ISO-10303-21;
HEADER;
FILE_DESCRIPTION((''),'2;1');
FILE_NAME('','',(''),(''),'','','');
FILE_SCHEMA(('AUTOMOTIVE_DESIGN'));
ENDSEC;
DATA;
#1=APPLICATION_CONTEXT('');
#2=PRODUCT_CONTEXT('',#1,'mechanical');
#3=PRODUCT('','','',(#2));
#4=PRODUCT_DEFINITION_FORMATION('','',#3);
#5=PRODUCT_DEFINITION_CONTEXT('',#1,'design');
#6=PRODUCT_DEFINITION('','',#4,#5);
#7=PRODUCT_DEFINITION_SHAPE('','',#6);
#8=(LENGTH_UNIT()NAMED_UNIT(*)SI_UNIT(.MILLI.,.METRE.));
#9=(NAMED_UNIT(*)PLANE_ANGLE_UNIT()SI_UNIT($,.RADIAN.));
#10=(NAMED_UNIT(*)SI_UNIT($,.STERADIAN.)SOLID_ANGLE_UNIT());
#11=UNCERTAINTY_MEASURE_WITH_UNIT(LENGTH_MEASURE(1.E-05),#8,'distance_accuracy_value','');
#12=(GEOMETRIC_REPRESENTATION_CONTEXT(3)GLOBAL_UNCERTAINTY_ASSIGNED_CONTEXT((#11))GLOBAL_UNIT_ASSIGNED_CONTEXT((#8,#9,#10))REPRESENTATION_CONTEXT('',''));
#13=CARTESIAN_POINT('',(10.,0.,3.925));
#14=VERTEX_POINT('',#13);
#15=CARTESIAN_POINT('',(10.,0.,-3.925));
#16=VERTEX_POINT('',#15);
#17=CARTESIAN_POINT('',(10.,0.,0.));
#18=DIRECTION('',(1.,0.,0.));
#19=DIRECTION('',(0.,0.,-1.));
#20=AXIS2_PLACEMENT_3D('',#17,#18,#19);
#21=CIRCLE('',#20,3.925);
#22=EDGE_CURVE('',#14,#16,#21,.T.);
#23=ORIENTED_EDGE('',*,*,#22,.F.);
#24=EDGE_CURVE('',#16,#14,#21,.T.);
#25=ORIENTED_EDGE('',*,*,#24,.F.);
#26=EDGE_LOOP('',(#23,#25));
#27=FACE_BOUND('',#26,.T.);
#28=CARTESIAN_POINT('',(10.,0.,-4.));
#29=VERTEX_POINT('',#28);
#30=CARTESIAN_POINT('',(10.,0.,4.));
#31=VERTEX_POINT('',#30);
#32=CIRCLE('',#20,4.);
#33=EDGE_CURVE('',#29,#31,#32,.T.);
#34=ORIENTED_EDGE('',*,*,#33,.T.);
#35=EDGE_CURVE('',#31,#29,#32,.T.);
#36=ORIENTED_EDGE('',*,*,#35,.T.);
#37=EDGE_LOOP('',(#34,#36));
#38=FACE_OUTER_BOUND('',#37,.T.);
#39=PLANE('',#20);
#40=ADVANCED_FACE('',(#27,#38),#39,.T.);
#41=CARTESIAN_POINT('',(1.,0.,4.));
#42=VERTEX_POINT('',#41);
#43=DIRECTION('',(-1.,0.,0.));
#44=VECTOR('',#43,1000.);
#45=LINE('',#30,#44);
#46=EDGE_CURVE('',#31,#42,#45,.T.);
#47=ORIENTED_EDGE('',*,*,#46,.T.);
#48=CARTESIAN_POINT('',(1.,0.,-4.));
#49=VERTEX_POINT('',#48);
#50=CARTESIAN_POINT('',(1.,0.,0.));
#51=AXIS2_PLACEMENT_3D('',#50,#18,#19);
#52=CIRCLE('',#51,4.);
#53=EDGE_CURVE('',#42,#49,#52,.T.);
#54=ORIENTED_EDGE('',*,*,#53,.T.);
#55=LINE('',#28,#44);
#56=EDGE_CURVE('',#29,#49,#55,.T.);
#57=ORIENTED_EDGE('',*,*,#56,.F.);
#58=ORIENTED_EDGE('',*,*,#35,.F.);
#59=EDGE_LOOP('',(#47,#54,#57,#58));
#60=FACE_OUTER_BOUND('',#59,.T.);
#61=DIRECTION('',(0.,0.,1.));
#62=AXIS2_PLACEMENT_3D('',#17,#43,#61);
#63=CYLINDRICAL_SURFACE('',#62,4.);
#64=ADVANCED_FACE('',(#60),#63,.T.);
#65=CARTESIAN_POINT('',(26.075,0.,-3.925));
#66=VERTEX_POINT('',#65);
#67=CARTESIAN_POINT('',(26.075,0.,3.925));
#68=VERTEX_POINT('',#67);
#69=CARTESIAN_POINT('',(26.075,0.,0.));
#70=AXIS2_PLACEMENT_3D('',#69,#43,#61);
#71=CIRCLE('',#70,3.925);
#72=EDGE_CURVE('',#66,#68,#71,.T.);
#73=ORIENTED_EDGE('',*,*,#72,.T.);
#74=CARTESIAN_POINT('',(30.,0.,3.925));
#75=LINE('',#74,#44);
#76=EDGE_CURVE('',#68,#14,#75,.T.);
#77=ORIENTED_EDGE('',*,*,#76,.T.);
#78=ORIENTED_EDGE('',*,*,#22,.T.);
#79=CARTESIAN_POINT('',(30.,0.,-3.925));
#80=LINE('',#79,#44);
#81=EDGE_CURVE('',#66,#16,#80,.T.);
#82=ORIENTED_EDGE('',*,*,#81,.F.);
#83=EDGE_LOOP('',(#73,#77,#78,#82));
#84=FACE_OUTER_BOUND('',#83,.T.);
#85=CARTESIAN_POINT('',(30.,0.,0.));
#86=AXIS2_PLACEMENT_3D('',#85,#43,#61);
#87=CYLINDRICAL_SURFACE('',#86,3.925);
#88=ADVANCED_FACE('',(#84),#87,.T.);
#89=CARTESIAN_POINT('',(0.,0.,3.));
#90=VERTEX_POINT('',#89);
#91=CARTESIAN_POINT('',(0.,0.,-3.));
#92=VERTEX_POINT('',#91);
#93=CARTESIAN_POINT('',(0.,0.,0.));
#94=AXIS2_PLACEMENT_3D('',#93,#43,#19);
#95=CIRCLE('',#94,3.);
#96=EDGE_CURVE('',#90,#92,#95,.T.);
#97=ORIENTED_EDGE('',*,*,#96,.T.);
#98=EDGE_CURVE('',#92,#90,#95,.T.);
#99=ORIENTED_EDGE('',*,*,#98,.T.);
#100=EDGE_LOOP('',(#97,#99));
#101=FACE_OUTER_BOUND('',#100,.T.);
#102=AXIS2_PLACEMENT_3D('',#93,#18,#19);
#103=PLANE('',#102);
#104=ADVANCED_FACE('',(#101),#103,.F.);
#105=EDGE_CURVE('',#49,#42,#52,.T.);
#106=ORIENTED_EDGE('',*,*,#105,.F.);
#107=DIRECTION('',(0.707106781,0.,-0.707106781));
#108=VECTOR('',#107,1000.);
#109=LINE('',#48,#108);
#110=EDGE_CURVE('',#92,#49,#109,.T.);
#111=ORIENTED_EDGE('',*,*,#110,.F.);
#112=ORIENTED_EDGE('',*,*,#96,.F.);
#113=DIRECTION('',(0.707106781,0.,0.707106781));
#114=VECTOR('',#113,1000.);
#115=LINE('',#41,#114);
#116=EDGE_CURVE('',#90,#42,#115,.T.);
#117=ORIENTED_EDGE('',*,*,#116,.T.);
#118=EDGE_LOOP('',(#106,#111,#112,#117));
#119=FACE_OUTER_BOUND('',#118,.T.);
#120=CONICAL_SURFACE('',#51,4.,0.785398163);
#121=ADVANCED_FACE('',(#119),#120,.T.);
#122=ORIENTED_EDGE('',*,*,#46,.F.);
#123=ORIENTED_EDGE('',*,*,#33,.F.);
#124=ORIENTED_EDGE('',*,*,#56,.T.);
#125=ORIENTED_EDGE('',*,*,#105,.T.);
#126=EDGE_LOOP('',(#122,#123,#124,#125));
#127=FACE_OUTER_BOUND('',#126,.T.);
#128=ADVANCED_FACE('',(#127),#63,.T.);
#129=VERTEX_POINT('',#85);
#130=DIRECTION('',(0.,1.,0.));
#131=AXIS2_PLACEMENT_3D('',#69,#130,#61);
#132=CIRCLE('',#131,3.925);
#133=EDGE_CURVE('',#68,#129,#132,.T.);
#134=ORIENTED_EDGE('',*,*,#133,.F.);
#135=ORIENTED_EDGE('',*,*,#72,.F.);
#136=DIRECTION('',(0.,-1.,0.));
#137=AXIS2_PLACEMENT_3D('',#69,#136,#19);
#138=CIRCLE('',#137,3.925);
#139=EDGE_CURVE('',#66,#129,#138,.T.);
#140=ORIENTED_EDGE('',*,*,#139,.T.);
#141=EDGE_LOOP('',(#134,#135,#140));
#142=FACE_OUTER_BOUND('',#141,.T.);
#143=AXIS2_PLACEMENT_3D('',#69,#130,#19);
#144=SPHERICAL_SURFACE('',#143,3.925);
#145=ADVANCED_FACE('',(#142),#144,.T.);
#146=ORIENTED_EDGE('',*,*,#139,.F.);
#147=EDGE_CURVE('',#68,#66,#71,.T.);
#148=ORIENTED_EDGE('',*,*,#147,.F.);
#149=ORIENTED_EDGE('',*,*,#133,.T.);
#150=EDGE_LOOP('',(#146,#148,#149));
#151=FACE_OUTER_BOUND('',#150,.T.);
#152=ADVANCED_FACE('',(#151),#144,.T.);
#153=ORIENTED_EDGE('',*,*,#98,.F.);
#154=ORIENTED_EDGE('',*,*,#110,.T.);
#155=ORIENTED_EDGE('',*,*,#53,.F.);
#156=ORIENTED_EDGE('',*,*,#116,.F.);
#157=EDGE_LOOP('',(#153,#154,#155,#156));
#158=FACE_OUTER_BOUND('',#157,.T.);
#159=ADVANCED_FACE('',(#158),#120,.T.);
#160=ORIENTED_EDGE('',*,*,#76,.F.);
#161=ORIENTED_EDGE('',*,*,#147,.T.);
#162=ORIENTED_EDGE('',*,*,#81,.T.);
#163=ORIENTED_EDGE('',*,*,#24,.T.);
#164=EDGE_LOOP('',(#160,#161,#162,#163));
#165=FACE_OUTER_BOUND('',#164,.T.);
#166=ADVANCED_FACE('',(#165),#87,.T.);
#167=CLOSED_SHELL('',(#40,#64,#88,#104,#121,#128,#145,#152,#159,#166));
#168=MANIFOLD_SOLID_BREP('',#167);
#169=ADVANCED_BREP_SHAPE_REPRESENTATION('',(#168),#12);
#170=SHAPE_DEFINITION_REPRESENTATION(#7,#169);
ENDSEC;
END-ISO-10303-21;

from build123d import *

# Parameters (mm, degrees)
SKETCH_1_R      = 4
EXTRUDE_1_DEPTH = 10
SKETCH_2_R      = 3.925
EXTRUDE_2_DEPTH = 20
FILLET_1_R      = 3.925
CHAMFER_1_SIZE  = 1


with BuildPart() as part:
    # 草图1 → 凸台-拉伸1 (new body)
    with BuildSketch(Plane(origin=(0, 0, 0), x_dir=(0, 0, -1), z_dir=(1, 0, 0))):
        Circle(SKETCH_1_R)
    extrude(amount=EXTRUDE_1_DEPTH)

    # 草图2 → 凸台-拉伸2 (add)
    with BuildSketch(Plane(origin=(10, 0, 0), x_dir=(0, 0, -1), z_dir=(1, 0, 0))):
        Circle(SKETCH_2_R)
    extrude(amount=EXTRUDE_2_DEPTH)

    # 圆角1
    fillet_1_edges = [part.edges().sort_by_distance(p)[0] for p in [
        (30, 0, 3.925),
    ]]
    fillet(fillet_1_edges, radius=FILLET_1_R)

    # 倒角1
    chamfer_1_edges = [part.edges().sort_by_distance(p)[0] for p in [
        (0, 0, 4),
    ]]
    chamfer(chamfer_1_edges, length=CHAMFER_1_SIZE)


solid = part.part
